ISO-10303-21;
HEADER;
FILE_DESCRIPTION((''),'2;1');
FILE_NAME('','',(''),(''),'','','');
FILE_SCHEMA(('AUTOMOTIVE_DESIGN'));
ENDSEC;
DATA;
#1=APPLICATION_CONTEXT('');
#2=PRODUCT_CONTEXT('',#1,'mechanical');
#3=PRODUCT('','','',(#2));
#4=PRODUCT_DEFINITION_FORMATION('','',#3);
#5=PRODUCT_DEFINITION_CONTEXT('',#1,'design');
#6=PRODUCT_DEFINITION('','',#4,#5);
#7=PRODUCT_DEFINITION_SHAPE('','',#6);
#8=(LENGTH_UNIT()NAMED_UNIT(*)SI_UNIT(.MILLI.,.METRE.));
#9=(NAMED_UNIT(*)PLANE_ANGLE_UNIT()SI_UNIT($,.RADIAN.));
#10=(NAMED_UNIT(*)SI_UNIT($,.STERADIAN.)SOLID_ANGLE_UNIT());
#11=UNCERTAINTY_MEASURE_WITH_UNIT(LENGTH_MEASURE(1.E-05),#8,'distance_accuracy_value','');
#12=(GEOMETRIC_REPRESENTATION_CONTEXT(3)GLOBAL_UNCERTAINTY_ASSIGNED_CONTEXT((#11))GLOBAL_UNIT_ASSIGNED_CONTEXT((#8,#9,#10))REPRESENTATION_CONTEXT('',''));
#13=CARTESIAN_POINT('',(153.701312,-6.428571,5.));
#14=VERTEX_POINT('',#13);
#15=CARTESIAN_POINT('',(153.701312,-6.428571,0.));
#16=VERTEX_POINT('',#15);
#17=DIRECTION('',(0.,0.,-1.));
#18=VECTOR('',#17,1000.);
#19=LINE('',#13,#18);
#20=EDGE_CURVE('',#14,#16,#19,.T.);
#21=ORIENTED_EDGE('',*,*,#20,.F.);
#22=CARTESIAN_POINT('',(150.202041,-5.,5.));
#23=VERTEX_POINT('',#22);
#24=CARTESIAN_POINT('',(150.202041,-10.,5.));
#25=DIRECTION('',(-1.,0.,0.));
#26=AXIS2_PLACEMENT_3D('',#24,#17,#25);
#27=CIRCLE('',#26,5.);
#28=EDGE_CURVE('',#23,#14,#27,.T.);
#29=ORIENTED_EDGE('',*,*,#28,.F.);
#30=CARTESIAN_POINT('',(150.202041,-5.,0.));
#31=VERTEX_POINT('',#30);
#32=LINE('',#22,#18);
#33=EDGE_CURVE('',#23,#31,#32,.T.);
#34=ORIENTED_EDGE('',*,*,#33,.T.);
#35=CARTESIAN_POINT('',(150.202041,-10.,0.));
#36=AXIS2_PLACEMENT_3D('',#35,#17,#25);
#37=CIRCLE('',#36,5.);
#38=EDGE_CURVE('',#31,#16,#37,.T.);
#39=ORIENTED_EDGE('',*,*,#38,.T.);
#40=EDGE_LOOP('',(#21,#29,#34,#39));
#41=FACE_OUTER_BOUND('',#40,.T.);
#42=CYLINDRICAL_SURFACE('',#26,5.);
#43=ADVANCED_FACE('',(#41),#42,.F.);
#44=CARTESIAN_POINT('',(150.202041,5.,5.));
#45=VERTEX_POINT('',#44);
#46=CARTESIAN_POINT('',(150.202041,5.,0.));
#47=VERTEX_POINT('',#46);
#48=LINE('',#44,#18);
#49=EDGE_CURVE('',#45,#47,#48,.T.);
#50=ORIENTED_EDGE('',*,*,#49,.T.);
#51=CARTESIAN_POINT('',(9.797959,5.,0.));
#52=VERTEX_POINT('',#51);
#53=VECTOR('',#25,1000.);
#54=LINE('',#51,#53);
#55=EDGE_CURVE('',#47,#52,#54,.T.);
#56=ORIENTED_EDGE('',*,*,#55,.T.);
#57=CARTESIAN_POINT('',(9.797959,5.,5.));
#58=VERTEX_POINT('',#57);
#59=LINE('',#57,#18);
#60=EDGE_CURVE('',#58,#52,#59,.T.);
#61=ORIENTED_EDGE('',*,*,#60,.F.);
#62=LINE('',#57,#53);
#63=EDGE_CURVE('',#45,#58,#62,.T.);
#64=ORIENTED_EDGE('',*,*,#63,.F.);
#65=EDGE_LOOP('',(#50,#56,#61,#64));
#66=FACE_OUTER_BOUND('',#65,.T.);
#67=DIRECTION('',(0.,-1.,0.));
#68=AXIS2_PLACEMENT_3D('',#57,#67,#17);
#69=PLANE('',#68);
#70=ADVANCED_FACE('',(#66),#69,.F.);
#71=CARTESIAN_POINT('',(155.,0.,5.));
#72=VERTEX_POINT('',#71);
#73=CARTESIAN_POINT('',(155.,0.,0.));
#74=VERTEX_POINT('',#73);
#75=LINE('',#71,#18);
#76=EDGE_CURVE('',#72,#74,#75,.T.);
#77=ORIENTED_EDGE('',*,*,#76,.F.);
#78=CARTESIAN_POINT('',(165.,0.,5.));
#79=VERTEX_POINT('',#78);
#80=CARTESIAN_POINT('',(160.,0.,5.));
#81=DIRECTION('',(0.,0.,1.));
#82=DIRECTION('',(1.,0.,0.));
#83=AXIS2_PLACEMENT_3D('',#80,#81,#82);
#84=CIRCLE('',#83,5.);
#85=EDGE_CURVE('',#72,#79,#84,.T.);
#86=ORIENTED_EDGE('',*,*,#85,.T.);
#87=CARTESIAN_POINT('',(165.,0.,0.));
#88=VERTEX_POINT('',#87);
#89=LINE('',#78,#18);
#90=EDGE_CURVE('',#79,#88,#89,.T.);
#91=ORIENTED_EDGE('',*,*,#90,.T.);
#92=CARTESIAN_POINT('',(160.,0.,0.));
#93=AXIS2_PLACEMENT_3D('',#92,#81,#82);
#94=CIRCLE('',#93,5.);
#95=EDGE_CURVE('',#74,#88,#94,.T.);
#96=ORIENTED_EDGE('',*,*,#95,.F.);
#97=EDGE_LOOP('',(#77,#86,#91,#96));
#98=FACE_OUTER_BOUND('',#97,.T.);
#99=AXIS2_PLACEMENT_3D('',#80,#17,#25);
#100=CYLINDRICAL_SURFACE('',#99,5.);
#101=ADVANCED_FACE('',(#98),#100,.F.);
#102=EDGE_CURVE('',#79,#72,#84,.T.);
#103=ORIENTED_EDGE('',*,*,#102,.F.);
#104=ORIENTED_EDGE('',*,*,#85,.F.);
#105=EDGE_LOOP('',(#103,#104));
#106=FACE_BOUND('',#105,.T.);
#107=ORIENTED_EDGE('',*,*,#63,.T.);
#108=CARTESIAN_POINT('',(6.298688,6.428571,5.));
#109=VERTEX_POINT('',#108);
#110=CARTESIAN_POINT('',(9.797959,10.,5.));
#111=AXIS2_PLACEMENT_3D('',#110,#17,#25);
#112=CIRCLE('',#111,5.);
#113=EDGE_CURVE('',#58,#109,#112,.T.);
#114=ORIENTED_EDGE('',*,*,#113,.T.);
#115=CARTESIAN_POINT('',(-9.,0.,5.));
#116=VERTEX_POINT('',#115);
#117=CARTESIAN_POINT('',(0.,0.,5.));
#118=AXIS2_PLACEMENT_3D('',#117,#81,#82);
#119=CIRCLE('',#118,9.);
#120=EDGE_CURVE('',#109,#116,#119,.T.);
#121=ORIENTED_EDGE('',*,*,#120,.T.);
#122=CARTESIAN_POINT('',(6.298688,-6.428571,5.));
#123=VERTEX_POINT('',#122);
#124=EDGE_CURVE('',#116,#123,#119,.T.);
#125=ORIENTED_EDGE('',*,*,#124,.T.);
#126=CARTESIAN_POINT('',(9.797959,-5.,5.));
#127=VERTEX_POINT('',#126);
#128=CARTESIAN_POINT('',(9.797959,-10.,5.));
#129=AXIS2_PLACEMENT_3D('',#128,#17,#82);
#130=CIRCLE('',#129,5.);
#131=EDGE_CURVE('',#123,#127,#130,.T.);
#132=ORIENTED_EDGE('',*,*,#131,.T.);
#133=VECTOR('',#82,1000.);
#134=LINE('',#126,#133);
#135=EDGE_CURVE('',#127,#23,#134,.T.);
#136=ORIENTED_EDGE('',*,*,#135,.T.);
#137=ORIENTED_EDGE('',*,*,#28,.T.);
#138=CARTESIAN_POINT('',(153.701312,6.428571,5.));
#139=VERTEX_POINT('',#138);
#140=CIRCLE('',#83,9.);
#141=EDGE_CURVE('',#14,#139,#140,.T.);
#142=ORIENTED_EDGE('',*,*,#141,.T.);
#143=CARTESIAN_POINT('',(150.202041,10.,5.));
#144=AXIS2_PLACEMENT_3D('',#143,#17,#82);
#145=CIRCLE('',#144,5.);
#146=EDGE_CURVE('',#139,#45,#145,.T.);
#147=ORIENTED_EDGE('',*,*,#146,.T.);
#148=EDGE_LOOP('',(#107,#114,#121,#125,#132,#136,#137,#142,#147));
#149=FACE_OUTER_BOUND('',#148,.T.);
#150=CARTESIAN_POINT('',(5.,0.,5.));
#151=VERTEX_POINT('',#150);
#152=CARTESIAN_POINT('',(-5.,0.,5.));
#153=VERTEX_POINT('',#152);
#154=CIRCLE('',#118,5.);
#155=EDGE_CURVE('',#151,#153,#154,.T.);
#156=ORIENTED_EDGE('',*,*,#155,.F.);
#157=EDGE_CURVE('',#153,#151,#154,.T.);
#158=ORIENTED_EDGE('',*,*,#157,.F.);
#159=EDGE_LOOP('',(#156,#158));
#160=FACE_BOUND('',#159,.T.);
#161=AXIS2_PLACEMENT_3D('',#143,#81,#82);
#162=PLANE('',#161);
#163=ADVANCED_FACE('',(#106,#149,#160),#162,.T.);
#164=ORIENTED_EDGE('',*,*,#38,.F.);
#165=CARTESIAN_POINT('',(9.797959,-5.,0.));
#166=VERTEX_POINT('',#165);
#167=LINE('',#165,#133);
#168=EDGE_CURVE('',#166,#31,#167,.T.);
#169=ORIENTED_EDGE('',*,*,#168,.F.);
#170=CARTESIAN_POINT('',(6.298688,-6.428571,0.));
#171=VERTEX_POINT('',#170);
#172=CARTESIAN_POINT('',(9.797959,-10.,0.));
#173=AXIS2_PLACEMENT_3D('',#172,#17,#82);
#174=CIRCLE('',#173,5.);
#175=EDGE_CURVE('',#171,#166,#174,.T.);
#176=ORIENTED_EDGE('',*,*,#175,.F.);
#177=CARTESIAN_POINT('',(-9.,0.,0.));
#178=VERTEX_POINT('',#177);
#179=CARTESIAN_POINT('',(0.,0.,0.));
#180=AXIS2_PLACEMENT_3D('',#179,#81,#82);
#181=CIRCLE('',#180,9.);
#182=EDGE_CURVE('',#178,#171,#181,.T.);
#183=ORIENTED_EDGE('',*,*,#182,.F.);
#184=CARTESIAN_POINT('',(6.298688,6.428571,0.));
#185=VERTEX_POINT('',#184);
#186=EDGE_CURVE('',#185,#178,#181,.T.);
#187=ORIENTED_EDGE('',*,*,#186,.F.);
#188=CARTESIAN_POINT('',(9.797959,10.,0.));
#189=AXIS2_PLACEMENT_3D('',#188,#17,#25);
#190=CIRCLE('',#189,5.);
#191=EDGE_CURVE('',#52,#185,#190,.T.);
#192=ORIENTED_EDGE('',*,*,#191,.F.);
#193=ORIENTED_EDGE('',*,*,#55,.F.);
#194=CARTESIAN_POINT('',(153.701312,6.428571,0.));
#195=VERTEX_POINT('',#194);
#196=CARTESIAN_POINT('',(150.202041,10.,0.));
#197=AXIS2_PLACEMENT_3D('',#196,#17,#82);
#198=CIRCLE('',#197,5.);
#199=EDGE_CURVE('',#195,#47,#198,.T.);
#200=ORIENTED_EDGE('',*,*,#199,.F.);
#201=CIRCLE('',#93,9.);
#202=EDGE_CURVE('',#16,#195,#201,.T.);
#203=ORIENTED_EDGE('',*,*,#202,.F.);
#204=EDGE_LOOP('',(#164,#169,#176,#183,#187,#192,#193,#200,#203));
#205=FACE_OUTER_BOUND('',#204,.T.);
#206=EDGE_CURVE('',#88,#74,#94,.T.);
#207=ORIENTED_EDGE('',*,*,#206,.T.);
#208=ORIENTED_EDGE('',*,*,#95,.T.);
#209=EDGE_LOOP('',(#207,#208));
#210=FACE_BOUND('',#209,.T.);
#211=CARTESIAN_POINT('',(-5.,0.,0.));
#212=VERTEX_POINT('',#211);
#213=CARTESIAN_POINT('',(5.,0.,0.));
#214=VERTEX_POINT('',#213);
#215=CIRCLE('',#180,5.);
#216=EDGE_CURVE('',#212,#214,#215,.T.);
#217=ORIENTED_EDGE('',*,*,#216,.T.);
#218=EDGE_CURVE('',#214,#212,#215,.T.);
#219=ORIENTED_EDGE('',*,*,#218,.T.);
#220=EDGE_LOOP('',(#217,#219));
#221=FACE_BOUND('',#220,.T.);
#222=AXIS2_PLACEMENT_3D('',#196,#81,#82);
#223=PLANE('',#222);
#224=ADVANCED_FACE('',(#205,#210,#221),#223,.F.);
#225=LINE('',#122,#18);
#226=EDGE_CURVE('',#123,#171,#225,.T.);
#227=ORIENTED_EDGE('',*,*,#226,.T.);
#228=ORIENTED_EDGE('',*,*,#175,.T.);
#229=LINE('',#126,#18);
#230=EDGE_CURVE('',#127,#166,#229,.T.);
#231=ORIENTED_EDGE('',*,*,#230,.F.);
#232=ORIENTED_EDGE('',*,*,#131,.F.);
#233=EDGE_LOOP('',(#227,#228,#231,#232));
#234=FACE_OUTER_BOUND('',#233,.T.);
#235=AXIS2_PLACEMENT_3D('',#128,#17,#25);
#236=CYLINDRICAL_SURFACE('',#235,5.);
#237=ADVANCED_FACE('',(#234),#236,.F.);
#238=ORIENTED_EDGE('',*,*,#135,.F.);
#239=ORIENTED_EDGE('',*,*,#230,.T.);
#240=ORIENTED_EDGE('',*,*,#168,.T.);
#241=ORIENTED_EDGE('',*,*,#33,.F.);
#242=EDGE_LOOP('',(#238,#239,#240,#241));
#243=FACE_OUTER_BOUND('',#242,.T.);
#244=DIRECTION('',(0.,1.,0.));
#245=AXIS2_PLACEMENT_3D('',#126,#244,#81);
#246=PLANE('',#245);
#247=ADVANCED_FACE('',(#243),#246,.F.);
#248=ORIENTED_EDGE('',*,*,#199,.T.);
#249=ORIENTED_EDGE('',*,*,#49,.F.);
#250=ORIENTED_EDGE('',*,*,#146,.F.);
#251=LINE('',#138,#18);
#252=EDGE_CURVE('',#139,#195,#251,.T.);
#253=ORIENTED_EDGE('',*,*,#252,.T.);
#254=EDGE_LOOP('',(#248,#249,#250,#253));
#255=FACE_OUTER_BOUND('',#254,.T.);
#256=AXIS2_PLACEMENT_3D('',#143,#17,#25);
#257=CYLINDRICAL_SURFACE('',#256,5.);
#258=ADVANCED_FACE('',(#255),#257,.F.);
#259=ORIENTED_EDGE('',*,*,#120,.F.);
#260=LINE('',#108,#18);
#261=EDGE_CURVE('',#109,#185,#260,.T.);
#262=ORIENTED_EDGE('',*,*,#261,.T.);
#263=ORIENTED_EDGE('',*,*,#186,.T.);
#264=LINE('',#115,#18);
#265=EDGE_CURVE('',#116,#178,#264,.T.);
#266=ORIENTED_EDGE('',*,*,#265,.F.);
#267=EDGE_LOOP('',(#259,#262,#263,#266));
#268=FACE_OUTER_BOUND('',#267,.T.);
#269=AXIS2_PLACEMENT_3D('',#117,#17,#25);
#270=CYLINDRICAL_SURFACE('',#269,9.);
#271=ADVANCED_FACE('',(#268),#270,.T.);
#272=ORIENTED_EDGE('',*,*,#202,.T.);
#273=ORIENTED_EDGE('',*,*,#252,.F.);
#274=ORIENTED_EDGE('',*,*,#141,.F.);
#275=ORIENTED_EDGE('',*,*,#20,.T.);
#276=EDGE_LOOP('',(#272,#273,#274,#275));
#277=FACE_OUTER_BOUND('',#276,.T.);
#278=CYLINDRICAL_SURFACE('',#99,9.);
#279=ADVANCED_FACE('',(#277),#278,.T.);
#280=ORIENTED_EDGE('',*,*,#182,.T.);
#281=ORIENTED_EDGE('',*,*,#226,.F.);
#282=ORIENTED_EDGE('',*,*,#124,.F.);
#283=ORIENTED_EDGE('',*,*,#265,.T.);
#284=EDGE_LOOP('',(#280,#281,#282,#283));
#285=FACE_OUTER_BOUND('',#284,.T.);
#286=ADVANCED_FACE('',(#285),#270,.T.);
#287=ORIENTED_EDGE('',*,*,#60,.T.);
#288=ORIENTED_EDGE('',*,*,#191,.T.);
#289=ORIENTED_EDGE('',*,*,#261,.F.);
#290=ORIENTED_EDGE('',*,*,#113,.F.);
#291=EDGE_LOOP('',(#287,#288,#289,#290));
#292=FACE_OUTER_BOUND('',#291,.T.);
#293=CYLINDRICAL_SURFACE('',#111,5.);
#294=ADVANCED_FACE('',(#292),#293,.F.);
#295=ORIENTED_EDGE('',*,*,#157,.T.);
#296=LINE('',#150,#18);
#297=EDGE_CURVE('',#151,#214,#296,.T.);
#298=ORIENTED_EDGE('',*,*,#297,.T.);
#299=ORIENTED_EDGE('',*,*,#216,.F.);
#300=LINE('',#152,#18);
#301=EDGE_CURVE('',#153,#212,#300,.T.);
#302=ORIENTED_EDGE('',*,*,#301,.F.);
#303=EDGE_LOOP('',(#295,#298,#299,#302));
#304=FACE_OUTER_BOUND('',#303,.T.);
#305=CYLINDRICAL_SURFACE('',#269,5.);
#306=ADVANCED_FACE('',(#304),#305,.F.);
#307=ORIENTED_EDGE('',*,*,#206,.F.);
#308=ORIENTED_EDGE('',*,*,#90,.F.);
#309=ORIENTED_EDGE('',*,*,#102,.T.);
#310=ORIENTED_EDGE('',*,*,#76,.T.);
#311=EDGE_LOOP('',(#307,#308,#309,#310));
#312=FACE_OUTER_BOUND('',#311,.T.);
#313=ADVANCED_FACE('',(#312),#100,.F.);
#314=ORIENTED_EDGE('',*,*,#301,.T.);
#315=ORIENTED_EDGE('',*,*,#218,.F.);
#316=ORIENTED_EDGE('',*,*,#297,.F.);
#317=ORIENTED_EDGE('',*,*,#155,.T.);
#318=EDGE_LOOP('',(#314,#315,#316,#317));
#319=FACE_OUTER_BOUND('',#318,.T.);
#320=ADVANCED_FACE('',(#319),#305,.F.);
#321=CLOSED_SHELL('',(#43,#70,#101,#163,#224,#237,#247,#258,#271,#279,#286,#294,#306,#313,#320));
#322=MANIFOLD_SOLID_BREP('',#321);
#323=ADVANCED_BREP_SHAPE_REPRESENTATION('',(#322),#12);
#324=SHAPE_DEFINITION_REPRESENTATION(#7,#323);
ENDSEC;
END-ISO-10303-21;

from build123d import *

# Parameters (mm, degrees)
SKETCH1_R           = 5
BOSS_EXTRUDE1_DEPTH = 5


with BuildPart() as part:
    # Sketch1 → Boss-Extrude1 (new body)
    with BuildSketch(Plane.XY):
        with BuildLine():
            Line((9.797958971, 5), (150.202041029, 5))
            ThreePointArc((150.202041029, 5), (152.091863394, 5.370899501), (153.70131209, 6.428571429))
            ThreePointArc((153.70131209, 6.428571429), (169, 0), (153.70131209, -6.428571429))
            ThreePointArc((153.70131209, -6.428571429), (152.091863394, -5.370899501), (150.202041029, -5))
            Line((150.202041029, -5), (9.797958971, -5))
            ThreePointArc((9.797958971, -5), (7.908136606, -5.370899501), (6.29868791, -6.428571429))
            ThreePointArc((6.29868791, -6.428571429), (-9, 0), (6.29868791, 6.428571429))
            ThreePointArc((6.29868791, 6.428571429), (7.908136606, 5.370899501), (9.797958971, 5))
        make_face()
        Circle(SKETCH1_R, mode=Mode.SUBTRACT)
        with Locations((160, 0)):
            Circle(SKETCH1_R, mode=Mode.SUBTRACT)
    extrude(amount=BOSS_EXTRUDE1_DEPTH)


solid = part.part
